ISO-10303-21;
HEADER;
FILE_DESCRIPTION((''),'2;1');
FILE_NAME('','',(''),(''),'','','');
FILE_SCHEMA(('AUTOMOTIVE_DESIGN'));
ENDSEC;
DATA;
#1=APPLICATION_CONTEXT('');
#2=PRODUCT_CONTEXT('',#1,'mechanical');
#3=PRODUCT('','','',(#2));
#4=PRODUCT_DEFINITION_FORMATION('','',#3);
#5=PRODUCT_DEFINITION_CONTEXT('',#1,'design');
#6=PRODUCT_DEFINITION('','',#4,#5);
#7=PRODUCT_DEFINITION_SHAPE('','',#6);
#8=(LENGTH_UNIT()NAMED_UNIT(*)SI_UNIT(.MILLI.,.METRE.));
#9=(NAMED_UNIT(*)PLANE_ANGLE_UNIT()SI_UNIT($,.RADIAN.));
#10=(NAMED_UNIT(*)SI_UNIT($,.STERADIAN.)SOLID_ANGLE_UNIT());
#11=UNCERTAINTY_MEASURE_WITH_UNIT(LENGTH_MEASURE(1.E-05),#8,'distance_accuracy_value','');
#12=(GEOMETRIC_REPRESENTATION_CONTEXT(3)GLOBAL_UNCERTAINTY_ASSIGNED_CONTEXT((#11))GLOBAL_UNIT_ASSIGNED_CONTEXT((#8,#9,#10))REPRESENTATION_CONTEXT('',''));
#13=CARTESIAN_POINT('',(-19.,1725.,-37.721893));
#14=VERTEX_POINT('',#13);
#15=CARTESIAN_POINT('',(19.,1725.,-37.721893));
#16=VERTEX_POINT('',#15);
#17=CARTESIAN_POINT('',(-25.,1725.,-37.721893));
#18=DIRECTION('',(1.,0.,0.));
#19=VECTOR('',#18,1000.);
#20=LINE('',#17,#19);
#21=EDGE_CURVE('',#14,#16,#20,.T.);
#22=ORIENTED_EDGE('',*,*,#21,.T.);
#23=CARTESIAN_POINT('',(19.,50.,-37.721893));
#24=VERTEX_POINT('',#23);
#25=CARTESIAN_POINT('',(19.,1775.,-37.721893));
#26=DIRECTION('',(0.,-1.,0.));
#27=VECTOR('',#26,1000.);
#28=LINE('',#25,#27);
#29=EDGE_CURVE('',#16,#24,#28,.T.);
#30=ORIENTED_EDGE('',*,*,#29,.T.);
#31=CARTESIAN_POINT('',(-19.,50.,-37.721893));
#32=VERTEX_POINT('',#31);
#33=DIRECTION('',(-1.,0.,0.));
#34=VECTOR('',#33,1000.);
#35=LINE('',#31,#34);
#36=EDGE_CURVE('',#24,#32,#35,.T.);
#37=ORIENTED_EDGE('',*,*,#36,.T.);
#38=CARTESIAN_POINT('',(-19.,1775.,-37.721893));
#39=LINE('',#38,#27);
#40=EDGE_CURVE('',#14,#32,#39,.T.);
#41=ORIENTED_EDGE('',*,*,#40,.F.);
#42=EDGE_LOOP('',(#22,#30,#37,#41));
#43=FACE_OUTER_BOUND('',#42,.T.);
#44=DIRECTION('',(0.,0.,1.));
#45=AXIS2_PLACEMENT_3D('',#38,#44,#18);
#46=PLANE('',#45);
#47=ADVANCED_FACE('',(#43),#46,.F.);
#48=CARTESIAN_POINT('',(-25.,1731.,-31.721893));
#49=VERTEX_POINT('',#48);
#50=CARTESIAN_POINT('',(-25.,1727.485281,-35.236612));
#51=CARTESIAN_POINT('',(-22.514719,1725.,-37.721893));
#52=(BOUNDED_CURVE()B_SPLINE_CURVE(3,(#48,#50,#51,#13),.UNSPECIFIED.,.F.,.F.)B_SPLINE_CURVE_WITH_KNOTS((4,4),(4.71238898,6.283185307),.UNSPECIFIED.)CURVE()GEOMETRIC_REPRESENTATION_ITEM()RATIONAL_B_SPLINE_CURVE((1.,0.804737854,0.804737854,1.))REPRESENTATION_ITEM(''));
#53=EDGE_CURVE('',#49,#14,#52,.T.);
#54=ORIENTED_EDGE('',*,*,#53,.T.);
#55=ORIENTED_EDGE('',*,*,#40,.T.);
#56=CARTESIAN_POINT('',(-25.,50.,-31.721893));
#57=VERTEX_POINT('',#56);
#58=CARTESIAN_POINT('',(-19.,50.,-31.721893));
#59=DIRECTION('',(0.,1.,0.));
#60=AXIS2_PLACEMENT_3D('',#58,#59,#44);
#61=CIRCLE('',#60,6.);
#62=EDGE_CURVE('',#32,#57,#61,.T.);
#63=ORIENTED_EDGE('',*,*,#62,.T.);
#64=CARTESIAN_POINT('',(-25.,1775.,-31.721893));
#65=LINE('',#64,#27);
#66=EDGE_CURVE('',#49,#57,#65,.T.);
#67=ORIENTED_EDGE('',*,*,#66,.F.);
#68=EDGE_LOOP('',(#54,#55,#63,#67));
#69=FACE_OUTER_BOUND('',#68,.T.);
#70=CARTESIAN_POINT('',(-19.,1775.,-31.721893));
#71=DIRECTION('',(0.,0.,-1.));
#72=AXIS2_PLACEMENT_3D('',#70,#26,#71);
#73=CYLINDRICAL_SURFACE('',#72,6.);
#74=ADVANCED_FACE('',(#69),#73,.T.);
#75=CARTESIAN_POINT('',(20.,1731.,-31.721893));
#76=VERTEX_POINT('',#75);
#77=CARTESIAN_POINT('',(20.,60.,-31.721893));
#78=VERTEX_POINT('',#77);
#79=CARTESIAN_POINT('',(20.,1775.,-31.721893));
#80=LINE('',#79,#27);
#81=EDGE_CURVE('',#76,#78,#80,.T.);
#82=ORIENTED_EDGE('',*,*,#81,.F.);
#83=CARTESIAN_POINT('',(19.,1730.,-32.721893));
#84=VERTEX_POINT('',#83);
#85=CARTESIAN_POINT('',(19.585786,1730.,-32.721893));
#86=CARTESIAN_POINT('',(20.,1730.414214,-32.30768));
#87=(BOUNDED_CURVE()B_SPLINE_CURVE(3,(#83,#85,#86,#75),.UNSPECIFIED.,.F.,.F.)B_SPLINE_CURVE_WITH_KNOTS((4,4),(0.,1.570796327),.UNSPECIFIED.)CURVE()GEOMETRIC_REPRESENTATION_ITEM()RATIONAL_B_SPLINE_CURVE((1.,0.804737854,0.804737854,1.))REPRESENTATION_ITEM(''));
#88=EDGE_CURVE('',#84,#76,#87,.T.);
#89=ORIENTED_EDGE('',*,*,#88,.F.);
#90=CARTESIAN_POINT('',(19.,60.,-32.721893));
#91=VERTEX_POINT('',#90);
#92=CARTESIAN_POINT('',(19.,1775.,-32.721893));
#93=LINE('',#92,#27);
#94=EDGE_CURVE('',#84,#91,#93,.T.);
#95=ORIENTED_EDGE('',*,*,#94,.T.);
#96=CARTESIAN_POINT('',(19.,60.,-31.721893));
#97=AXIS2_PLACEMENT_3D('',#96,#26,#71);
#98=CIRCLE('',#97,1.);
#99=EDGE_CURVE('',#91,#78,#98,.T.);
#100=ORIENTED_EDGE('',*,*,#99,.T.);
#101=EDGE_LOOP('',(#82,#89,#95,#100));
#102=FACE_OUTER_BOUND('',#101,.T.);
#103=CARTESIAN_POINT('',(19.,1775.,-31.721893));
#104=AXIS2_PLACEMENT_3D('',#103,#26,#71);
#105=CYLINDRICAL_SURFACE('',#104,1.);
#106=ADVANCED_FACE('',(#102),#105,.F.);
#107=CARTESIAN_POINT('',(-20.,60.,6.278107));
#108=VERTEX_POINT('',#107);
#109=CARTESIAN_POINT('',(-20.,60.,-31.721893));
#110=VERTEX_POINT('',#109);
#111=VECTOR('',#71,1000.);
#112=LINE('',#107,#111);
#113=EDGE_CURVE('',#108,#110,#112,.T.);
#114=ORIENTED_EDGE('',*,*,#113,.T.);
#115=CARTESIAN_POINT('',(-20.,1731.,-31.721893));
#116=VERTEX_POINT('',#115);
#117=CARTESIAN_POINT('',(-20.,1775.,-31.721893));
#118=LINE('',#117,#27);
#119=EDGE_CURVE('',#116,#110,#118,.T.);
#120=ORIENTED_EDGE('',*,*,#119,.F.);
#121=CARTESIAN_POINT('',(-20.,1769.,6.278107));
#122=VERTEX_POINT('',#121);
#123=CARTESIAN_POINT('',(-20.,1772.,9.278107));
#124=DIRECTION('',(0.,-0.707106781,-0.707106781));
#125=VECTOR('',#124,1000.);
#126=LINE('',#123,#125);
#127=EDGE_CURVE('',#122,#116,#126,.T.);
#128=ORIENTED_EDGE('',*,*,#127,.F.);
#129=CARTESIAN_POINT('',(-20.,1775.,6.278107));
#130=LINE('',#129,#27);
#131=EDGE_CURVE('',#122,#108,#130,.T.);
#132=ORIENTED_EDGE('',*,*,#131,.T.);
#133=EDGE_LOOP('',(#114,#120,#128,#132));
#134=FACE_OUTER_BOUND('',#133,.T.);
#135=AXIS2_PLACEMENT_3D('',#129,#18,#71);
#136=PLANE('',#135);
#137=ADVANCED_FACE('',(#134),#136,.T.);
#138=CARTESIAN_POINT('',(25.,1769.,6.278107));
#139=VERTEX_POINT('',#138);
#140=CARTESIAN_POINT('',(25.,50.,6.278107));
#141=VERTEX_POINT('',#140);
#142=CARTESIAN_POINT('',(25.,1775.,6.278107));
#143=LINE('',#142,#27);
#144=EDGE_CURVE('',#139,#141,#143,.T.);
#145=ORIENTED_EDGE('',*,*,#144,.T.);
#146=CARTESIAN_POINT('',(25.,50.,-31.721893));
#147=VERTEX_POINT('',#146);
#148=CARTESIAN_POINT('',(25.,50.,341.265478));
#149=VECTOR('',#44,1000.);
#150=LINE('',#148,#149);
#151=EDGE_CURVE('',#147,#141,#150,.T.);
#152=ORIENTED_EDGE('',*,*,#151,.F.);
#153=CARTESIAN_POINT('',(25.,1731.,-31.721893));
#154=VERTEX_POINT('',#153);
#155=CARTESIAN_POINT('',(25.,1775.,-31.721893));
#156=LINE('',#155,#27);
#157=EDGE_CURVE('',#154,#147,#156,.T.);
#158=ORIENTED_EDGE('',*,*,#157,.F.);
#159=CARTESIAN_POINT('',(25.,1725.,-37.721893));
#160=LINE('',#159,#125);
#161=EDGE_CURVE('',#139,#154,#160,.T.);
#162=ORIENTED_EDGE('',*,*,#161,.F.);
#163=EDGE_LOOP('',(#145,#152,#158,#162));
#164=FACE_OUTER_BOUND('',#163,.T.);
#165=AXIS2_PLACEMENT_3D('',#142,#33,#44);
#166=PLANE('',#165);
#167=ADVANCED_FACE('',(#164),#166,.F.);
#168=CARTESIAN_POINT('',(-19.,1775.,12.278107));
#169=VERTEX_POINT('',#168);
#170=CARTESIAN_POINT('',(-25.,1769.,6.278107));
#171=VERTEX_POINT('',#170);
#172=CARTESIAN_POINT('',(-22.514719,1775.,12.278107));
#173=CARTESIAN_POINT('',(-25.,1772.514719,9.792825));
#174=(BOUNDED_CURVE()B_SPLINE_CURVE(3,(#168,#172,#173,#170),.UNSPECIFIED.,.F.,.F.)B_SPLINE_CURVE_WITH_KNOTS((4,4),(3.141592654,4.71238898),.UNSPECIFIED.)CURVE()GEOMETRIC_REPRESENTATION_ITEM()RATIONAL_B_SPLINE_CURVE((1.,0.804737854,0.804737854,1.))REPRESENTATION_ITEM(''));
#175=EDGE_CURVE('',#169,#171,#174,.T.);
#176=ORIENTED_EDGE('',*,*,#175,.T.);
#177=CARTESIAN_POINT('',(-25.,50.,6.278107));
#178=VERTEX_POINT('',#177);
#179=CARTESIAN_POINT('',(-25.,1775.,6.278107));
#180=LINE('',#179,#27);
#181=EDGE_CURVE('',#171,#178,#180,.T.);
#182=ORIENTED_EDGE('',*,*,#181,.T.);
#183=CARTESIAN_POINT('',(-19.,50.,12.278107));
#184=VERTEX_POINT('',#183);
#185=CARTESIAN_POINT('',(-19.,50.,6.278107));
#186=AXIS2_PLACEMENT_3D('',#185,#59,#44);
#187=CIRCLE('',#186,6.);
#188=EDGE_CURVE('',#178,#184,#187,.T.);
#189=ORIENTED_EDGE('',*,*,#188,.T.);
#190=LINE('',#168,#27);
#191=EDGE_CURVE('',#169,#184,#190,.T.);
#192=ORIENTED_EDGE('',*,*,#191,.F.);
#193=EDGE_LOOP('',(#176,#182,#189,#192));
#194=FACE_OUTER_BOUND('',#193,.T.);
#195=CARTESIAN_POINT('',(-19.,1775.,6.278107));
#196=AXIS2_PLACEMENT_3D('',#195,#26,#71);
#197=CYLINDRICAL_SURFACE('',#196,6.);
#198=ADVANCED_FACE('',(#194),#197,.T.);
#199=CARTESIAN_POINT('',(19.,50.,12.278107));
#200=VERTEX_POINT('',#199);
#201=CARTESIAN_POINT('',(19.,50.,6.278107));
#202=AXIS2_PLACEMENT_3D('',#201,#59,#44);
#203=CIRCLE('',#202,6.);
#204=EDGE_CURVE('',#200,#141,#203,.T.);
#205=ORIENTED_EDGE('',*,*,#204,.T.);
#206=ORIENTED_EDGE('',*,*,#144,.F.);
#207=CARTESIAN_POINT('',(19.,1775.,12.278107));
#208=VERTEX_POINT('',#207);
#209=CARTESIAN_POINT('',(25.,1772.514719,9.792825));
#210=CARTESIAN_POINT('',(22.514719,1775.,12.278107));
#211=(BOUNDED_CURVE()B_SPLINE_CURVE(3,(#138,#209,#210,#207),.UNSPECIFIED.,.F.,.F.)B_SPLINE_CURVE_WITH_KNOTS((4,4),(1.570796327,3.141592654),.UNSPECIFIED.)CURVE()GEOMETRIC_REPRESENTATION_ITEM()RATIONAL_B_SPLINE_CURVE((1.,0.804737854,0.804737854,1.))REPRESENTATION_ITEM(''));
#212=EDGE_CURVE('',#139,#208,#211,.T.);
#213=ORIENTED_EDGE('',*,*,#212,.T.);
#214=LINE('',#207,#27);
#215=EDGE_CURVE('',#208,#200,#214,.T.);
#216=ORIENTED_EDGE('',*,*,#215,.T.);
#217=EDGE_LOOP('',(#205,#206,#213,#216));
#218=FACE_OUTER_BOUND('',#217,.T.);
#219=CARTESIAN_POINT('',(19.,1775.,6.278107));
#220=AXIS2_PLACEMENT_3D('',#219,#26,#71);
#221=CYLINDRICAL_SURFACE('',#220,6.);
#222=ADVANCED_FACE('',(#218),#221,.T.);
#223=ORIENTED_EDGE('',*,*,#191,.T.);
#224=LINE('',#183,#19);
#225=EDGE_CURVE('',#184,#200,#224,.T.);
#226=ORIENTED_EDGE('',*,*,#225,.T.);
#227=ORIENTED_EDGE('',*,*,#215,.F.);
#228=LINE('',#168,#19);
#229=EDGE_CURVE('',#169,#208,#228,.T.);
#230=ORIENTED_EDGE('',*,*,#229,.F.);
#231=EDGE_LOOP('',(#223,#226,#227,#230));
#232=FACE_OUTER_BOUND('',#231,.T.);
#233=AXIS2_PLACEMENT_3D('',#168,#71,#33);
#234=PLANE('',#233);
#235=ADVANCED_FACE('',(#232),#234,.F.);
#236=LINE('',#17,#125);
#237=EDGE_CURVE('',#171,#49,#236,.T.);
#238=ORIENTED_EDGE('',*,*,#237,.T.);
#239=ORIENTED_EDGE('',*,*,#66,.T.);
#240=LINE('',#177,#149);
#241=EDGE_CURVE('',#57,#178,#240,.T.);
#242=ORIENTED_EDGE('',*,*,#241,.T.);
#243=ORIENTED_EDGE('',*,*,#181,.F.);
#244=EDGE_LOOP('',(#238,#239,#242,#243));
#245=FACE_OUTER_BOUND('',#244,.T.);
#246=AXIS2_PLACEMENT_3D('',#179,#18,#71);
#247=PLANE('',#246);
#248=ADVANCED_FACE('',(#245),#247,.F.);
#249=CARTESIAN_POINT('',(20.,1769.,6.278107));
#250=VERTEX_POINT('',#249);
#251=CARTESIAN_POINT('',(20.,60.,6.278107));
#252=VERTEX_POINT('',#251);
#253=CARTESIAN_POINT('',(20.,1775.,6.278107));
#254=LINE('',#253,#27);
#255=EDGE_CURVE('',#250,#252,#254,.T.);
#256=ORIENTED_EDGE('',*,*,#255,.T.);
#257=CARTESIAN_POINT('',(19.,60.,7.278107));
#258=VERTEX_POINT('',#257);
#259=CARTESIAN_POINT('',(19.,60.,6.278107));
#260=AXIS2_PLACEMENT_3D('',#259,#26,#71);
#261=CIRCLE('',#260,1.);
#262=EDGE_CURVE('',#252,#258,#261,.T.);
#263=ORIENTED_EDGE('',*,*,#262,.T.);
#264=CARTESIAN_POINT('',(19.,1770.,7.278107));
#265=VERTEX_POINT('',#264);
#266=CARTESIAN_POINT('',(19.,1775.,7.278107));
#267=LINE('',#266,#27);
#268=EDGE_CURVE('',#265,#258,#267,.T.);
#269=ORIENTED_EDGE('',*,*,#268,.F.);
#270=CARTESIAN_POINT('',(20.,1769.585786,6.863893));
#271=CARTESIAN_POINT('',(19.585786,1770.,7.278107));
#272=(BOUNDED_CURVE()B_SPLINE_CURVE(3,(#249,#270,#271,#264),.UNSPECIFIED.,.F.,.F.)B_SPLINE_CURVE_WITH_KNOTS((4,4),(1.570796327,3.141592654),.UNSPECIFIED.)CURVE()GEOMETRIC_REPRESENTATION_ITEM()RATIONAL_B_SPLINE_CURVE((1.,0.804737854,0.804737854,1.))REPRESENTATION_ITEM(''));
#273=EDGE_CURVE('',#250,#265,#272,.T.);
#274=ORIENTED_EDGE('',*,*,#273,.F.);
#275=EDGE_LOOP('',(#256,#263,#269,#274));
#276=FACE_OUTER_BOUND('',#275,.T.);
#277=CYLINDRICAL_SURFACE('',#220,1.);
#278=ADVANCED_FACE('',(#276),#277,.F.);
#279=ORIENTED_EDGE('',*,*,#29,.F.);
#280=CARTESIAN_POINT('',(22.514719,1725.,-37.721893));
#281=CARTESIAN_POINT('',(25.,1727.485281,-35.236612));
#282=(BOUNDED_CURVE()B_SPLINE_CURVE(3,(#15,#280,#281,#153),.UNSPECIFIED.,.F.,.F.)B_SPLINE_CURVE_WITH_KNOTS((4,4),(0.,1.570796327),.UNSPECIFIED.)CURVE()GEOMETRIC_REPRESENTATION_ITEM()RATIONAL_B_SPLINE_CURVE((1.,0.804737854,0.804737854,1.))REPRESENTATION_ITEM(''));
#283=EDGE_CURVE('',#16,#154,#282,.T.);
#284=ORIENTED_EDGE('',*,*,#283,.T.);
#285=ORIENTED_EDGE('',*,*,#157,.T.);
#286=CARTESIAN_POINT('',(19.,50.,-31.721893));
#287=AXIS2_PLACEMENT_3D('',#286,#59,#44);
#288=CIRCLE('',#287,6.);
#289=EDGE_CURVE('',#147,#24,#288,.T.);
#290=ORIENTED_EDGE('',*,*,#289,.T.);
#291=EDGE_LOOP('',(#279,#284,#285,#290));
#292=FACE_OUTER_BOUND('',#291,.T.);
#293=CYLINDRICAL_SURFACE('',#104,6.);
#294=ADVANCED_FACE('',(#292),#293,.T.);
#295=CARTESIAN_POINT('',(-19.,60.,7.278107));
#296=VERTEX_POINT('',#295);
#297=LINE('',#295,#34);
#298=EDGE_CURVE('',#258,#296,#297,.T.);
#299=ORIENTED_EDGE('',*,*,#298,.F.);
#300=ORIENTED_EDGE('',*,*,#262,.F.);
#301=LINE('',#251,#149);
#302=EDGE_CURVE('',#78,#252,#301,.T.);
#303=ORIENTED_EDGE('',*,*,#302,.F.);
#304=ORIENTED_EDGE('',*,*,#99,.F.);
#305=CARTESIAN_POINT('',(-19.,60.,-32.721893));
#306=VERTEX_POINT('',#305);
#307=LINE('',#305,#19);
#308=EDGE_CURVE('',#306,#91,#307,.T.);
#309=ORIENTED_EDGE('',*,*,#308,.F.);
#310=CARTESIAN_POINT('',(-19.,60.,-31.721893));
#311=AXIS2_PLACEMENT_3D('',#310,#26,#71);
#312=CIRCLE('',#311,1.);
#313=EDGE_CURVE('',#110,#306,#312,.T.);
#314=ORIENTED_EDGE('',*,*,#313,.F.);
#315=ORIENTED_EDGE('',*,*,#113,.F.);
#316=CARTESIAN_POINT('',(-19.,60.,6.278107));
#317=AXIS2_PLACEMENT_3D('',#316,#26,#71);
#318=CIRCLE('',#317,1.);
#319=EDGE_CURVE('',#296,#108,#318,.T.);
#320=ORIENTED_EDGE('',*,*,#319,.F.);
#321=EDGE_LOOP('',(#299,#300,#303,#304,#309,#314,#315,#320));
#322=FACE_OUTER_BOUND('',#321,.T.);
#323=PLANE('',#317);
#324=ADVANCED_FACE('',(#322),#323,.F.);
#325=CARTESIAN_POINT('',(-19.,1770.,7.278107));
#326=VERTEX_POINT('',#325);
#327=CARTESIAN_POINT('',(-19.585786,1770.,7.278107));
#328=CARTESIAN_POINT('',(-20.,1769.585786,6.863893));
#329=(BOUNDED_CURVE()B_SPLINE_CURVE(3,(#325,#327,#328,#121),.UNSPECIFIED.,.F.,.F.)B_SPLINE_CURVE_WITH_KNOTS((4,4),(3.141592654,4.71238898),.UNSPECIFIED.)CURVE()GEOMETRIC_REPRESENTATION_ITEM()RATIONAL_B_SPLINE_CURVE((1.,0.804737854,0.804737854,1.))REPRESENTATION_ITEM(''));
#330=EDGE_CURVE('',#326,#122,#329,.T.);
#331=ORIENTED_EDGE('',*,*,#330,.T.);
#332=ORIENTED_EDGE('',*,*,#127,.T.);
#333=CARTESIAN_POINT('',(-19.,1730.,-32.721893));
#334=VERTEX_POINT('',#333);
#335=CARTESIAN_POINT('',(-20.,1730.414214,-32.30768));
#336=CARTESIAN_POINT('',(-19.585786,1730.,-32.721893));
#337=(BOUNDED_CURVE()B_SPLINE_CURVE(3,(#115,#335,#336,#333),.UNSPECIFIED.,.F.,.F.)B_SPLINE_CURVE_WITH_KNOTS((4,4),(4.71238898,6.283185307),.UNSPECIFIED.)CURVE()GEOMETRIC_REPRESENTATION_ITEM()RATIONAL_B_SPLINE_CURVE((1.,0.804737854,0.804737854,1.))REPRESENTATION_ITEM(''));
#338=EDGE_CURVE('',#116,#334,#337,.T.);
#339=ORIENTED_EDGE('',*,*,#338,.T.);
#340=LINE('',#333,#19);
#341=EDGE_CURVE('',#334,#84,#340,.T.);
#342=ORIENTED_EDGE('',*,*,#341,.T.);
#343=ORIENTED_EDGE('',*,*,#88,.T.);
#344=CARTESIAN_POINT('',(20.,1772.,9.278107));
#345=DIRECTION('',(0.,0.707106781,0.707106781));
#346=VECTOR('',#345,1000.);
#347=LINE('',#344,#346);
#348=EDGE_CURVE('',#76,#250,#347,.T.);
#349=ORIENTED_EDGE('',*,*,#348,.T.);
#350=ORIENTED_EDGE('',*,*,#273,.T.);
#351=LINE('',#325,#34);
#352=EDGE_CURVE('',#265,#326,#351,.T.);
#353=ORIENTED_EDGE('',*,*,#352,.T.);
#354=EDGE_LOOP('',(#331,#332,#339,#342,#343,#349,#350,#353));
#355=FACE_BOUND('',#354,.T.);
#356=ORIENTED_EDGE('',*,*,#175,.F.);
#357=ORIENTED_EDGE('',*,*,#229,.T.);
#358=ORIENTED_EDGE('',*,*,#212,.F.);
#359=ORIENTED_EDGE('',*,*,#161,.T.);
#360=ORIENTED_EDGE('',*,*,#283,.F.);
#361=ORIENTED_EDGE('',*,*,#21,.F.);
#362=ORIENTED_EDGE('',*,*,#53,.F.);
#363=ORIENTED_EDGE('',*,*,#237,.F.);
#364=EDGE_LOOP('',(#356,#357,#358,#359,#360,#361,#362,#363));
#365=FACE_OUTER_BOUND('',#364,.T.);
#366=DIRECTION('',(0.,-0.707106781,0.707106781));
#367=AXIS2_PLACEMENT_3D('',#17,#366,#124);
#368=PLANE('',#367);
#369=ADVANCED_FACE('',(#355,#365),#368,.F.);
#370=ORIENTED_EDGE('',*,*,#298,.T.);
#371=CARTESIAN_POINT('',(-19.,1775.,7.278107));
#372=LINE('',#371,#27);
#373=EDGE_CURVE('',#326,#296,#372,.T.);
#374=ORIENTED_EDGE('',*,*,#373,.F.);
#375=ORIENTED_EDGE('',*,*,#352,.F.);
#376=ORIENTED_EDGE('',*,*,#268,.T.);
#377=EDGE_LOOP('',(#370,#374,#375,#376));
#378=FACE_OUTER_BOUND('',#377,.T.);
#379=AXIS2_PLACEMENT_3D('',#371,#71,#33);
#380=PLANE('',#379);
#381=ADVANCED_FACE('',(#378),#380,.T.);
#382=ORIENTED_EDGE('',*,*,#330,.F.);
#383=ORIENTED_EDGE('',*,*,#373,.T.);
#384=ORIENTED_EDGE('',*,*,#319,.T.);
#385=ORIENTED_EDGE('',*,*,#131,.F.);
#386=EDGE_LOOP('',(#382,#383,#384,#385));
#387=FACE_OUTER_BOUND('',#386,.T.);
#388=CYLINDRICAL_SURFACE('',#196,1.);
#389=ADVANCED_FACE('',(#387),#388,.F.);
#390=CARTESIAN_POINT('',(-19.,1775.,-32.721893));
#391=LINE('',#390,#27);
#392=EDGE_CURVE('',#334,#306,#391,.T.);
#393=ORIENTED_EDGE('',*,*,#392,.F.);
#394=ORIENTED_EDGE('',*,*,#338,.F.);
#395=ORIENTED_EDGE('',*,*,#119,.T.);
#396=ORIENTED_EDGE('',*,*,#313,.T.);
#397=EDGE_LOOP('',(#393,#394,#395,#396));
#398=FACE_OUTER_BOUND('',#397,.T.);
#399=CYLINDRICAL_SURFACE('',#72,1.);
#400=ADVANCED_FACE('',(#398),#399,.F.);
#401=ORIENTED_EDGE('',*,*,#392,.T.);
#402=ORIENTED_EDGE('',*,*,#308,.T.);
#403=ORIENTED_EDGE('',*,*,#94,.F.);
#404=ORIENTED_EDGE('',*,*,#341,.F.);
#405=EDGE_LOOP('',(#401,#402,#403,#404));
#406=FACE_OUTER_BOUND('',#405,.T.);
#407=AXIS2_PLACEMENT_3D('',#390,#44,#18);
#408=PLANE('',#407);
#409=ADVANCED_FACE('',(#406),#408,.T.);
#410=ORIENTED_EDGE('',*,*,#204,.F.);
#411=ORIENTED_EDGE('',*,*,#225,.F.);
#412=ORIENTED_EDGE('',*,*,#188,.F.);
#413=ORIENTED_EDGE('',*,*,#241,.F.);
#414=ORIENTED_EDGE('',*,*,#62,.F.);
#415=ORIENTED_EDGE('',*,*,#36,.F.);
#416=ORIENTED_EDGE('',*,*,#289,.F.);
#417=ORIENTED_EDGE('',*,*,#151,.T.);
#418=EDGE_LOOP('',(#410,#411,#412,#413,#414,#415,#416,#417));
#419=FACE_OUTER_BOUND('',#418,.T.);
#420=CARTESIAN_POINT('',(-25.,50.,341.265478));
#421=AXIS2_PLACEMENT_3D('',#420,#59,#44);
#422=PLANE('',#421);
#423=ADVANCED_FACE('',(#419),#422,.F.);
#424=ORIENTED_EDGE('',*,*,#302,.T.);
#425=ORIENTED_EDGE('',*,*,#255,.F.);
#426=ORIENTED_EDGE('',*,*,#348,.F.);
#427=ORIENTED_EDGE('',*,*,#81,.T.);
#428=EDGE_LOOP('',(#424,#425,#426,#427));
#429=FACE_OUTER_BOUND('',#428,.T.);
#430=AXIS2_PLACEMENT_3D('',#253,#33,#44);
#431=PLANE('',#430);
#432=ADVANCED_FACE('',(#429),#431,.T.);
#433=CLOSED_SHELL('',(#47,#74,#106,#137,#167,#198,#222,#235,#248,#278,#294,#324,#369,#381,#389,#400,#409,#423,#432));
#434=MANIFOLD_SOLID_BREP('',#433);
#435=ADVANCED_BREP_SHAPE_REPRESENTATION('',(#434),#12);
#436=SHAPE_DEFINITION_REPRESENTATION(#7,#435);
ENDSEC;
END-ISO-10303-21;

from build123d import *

# Parameters (mm, degrees)
EXTRUDE_1_DEPTH     = 1775
CUT_EXTRUDE_1_DEPTH = 1777.104710103
EXTRUDE_2_DEPTH     = 5
SKETCH_4_W          = 596.189257656
SKETCH_4_H          = 322.935847897
CUT_EXTRUDE_2_DEPTH = 1777.104710103
EXTRUDE_3_DEPTH     = 10


with BuildPart() as part:
    # 草图1 → 凸台-拉伸1 (new body)
    with BuildSketch(Plane(origin=(0, 0, 0), x_dir=(1, 0, 0), z_dir=(0, 1, 0))):
        with BuildLine():
            Line((-19, -12.278106509), (19, -12.278106509))
            ThreePointArc((19, -12.278106509), (23.242640687, -10.520747196), (25, -6.278106509))
            Line((25, -6.278106509), (25, 31.721893491))
            ThreePointArc((25, 31.721893491), (23.242640687, 35.964534178), (19, 37.721893491))
            Line((19, 37.721893491), (-19, 37.721893491))
            ThreePointArc((-19, 37.721893491), (-23.242640687, 35.964534178), (-25, 31.721893491))
            Line((-25, 31.721893491), (-25, -6.278106509))
            ThreePointArc((-25, -6.278106509), (-23.242640687, -10.520747196), (-19, -12.278106509))
        make_face()
        with BuildLine():
            Line((-19, -7.278106509), (19, -7.278106509))
            ThreePointArc((19, -7.278106509), (19.707106781, -6.98521329), (20, -6.278106509))
            Line((20, -6.278106509), (20, 31.721893491))
            ThreePointArc((20, 31.721893491), (19.707106781, 32.429000272), (19, 32.721893491))
            Line((19, 32.721893491), (-19, 32.721893491))
            ThreePointArc((-19, 32.721893491), (-19.707106781, 32.429000272), (-20, 31.721893491))
            Line((-20, 31.721893491), (-20, -6.278106509))
            ThreePointArc((-20, -6.278106509), (-19.707106781, -6.98521329), (-19, -7.278106509))
        make_face(mode=Mode.SUBTRACT)
    extrude(amount=EXTRUDE_1_DEPTH)

    # 草图2 → 切除-拉伸1 (cut, through all)
    with BuildSketch(Plane(origin=(25, 0, 0), x_dir=(0, 0, -1), z_dir=(1, 0, 0))):
        Polygon((-12.278106509, 1775), (37.721893491, 1775), (37.721893491, 1725), align=None)
    extrude(amount=-CUT_EXTRUDE_1_DEPTH, mode=Mode.SUBTRACT)

    # 草图3 → 凸台-拉伸2 (add)
    with BuildSketch(Plane.XZ):
        with BuildLine():
            Line((-25, 6.278106509), (-25, -31.721893491))
            ThreePointArc((-25, -31.721893491), (-23.242640687, -35.964534178), (-19, -37.721893491))
            Line((-19, -37.721893491), (19, -37.721893491))
            ThreePointArc((19, -37.721893491), (23.242640687, -35.964534178), (25, -31.721893491))
            Line((25, -31.721893491), (25, 6.278106509))
            ThreePointArc((25, 6.278106509), (23.242640687, 10.520747196), (19, 12.278106509))
            Line((19, 12.278106509), (-19, 12.278106509))
            ThreePointArc((-19, 12.278106509), (-23.242640687, 10.520747196), (-25, 6.278106509))
        make_face()
    extrude(amount=-EXTRUDE_2_DEPTH)

    # 草图4 → 切除-拉伸2 (cut, through all)
    with BuildSketch(Plane(origin=(25, 0, 0), x_dir=(0, 0, -1), z_dir=(1, 0, 0))):
        with Locations((-43.170849414, -111.467923949)):
            Rectangle(SKETCH_4_W, SKETCH_4_H)
    extrude(amount=-CUT_EXTRUDE_2_DEPTH, mode=Mode.SUBTRACT)

    # 草图5 → 凸台-拉伸3 (add)
    with BuildSketch(Plane.XZ.offset(-50)):
        with BuildLine():
            Line((-25, 6.278106509), (-25, -31.721893491))
            ThreePointArc((-25, -31.721893491), (-23.242640687, -35.964534178), (-19, -37.721893491))
            Line((-19, -37.721893491), (19, -37.721893491))
            ThreePointArc((19, -37.721893491), (23.242640687, -35.964534178), (25, -31.721893491))
            Line((25, -31.721893491), (25, 6.278106509))
            ThreePointArc((25, 6.278106509), (23.242640687, 10.520747196), (19, 12.278106509))
            Line((19, 12.278106509), (-19, 12.278106509))
            ThreePointArc((-19, 12.278106509), (-23.242640687, 10.520747196), (-25, 6.278106509))
        make_face()
    extrude(amount=-EXTRUDE_3_DEPTH)


solid = part.part
